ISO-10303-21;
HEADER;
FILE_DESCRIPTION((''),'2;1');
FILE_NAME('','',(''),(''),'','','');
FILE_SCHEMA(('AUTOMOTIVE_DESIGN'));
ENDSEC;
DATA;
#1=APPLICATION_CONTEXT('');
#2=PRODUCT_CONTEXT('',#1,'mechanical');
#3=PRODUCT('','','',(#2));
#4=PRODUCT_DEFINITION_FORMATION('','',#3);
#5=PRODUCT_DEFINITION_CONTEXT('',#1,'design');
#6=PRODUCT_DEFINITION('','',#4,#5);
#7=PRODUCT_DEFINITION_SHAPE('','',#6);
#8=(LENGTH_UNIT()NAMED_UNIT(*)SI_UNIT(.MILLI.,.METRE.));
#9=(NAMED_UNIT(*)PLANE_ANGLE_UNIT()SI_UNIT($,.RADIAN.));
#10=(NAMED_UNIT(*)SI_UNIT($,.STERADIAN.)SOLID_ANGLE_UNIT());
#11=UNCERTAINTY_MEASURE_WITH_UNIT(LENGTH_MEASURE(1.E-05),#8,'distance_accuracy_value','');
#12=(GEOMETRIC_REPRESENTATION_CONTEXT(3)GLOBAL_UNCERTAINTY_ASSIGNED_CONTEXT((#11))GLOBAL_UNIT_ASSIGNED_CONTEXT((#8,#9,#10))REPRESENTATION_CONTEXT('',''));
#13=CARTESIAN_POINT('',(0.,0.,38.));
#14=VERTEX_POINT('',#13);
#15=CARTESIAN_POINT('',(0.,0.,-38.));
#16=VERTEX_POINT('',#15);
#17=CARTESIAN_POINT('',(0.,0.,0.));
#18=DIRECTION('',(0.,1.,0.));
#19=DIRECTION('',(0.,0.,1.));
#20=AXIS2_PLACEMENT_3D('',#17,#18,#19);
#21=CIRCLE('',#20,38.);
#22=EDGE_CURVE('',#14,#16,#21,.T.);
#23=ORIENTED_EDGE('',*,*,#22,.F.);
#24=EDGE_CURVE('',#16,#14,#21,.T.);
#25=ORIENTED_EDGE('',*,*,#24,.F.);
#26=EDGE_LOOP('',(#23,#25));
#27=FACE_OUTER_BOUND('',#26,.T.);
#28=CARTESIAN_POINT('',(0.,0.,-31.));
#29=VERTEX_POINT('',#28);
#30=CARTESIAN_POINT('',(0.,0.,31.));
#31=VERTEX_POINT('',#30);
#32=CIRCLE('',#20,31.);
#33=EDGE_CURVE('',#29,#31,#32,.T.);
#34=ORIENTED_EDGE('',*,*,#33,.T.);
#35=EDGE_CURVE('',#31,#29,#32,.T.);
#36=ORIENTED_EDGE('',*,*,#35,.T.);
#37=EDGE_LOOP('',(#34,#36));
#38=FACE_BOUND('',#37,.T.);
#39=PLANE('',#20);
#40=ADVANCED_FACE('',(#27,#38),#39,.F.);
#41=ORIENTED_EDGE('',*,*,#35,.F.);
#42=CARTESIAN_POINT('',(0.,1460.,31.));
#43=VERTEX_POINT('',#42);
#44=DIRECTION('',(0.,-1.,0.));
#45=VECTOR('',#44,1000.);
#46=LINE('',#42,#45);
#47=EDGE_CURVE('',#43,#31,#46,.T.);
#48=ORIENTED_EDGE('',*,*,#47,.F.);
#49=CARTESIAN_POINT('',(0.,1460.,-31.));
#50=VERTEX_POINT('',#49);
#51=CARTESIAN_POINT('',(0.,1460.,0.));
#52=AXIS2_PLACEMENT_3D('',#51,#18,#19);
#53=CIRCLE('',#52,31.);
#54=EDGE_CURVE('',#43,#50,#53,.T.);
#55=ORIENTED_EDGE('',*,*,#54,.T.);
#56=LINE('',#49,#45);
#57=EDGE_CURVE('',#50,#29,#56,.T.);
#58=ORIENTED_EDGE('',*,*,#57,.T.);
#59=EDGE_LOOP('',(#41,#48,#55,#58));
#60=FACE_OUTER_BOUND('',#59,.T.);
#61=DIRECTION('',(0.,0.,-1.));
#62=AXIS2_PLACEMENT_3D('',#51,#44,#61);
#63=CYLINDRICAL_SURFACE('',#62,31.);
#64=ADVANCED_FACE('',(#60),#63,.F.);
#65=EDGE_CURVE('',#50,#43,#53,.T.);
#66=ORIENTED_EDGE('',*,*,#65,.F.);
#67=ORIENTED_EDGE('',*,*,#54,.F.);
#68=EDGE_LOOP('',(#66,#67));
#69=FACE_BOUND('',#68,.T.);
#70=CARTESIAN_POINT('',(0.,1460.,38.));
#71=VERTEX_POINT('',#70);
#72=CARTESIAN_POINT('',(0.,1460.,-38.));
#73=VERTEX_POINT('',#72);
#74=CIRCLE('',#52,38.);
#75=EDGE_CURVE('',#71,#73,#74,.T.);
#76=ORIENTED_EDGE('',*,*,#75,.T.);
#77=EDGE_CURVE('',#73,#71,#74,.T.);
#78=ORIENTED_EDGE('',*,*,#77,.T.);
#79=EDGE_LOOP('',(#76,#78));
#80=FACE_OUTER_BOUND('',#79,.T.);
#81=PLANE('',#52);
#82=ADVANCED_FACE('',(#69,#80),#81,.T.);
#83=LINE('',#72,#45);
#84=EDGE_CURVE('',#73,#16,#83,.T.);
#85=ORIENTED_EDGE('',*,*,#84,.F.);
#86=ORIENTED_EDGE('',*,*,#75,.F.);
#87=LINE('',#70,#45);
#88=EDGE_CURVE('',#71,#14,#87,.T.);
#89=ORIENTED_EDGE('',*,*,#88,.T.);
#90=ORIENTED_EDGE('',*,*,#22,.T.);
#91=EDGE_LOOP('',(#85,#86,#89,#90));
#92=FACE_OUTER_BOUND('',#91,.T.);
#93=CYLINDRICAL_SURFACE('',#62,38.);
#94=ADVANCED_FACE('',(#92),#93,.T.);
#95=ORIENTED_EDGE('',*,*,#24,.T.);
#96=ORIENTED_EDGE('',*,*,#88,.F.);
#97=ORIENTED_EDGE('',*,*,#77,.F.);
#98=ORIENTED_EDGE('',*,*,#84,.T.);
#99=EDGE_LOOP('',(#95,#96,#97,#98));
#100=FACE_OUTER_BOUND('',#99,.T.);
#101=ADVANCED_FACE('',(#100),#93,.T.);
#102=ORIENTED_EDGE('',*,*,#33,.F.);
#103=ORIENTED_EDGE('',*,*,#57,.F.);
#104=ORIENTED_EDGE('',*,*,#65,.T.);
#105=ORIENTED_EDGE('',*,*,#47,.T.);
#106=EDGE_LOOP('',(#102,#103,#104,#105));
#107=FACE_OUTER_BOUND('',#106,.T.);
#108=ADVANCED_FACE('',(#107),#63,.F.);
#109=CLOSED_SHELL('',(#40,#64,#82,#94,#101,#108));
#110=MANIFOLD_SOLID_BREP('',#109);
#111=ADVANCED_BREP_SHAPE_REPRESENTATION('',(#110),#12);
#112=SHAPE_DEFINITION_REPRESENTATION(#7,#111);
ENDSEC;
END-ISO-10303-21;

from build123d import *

# Parameters (mm, degrees)
SKETCH1_R                              = 38
SKETCH1_R_2                            = 31
GB_T_6728_2002_ROUND_TUBE_76_7_1_DEPTH = 1460


with BuildPart() as part:
    # Sketch1 → Gb/t 6728-2002 round tube 76×7(1) (new body)
    with BuildSketch(Plane(origin=(0, 0, 0), x_dir=(-1, 0, 0), z_dir=(0, 1, 0))):
        Circle(SKETCH1_R)
        Circle(SKETCH1_R_2, mode=Mode.SUBTRACT)
    extrude(amount=GB_T_6728_2002_ROUND_TUBE_76_7_1_DEPTH)


solid = part.part
